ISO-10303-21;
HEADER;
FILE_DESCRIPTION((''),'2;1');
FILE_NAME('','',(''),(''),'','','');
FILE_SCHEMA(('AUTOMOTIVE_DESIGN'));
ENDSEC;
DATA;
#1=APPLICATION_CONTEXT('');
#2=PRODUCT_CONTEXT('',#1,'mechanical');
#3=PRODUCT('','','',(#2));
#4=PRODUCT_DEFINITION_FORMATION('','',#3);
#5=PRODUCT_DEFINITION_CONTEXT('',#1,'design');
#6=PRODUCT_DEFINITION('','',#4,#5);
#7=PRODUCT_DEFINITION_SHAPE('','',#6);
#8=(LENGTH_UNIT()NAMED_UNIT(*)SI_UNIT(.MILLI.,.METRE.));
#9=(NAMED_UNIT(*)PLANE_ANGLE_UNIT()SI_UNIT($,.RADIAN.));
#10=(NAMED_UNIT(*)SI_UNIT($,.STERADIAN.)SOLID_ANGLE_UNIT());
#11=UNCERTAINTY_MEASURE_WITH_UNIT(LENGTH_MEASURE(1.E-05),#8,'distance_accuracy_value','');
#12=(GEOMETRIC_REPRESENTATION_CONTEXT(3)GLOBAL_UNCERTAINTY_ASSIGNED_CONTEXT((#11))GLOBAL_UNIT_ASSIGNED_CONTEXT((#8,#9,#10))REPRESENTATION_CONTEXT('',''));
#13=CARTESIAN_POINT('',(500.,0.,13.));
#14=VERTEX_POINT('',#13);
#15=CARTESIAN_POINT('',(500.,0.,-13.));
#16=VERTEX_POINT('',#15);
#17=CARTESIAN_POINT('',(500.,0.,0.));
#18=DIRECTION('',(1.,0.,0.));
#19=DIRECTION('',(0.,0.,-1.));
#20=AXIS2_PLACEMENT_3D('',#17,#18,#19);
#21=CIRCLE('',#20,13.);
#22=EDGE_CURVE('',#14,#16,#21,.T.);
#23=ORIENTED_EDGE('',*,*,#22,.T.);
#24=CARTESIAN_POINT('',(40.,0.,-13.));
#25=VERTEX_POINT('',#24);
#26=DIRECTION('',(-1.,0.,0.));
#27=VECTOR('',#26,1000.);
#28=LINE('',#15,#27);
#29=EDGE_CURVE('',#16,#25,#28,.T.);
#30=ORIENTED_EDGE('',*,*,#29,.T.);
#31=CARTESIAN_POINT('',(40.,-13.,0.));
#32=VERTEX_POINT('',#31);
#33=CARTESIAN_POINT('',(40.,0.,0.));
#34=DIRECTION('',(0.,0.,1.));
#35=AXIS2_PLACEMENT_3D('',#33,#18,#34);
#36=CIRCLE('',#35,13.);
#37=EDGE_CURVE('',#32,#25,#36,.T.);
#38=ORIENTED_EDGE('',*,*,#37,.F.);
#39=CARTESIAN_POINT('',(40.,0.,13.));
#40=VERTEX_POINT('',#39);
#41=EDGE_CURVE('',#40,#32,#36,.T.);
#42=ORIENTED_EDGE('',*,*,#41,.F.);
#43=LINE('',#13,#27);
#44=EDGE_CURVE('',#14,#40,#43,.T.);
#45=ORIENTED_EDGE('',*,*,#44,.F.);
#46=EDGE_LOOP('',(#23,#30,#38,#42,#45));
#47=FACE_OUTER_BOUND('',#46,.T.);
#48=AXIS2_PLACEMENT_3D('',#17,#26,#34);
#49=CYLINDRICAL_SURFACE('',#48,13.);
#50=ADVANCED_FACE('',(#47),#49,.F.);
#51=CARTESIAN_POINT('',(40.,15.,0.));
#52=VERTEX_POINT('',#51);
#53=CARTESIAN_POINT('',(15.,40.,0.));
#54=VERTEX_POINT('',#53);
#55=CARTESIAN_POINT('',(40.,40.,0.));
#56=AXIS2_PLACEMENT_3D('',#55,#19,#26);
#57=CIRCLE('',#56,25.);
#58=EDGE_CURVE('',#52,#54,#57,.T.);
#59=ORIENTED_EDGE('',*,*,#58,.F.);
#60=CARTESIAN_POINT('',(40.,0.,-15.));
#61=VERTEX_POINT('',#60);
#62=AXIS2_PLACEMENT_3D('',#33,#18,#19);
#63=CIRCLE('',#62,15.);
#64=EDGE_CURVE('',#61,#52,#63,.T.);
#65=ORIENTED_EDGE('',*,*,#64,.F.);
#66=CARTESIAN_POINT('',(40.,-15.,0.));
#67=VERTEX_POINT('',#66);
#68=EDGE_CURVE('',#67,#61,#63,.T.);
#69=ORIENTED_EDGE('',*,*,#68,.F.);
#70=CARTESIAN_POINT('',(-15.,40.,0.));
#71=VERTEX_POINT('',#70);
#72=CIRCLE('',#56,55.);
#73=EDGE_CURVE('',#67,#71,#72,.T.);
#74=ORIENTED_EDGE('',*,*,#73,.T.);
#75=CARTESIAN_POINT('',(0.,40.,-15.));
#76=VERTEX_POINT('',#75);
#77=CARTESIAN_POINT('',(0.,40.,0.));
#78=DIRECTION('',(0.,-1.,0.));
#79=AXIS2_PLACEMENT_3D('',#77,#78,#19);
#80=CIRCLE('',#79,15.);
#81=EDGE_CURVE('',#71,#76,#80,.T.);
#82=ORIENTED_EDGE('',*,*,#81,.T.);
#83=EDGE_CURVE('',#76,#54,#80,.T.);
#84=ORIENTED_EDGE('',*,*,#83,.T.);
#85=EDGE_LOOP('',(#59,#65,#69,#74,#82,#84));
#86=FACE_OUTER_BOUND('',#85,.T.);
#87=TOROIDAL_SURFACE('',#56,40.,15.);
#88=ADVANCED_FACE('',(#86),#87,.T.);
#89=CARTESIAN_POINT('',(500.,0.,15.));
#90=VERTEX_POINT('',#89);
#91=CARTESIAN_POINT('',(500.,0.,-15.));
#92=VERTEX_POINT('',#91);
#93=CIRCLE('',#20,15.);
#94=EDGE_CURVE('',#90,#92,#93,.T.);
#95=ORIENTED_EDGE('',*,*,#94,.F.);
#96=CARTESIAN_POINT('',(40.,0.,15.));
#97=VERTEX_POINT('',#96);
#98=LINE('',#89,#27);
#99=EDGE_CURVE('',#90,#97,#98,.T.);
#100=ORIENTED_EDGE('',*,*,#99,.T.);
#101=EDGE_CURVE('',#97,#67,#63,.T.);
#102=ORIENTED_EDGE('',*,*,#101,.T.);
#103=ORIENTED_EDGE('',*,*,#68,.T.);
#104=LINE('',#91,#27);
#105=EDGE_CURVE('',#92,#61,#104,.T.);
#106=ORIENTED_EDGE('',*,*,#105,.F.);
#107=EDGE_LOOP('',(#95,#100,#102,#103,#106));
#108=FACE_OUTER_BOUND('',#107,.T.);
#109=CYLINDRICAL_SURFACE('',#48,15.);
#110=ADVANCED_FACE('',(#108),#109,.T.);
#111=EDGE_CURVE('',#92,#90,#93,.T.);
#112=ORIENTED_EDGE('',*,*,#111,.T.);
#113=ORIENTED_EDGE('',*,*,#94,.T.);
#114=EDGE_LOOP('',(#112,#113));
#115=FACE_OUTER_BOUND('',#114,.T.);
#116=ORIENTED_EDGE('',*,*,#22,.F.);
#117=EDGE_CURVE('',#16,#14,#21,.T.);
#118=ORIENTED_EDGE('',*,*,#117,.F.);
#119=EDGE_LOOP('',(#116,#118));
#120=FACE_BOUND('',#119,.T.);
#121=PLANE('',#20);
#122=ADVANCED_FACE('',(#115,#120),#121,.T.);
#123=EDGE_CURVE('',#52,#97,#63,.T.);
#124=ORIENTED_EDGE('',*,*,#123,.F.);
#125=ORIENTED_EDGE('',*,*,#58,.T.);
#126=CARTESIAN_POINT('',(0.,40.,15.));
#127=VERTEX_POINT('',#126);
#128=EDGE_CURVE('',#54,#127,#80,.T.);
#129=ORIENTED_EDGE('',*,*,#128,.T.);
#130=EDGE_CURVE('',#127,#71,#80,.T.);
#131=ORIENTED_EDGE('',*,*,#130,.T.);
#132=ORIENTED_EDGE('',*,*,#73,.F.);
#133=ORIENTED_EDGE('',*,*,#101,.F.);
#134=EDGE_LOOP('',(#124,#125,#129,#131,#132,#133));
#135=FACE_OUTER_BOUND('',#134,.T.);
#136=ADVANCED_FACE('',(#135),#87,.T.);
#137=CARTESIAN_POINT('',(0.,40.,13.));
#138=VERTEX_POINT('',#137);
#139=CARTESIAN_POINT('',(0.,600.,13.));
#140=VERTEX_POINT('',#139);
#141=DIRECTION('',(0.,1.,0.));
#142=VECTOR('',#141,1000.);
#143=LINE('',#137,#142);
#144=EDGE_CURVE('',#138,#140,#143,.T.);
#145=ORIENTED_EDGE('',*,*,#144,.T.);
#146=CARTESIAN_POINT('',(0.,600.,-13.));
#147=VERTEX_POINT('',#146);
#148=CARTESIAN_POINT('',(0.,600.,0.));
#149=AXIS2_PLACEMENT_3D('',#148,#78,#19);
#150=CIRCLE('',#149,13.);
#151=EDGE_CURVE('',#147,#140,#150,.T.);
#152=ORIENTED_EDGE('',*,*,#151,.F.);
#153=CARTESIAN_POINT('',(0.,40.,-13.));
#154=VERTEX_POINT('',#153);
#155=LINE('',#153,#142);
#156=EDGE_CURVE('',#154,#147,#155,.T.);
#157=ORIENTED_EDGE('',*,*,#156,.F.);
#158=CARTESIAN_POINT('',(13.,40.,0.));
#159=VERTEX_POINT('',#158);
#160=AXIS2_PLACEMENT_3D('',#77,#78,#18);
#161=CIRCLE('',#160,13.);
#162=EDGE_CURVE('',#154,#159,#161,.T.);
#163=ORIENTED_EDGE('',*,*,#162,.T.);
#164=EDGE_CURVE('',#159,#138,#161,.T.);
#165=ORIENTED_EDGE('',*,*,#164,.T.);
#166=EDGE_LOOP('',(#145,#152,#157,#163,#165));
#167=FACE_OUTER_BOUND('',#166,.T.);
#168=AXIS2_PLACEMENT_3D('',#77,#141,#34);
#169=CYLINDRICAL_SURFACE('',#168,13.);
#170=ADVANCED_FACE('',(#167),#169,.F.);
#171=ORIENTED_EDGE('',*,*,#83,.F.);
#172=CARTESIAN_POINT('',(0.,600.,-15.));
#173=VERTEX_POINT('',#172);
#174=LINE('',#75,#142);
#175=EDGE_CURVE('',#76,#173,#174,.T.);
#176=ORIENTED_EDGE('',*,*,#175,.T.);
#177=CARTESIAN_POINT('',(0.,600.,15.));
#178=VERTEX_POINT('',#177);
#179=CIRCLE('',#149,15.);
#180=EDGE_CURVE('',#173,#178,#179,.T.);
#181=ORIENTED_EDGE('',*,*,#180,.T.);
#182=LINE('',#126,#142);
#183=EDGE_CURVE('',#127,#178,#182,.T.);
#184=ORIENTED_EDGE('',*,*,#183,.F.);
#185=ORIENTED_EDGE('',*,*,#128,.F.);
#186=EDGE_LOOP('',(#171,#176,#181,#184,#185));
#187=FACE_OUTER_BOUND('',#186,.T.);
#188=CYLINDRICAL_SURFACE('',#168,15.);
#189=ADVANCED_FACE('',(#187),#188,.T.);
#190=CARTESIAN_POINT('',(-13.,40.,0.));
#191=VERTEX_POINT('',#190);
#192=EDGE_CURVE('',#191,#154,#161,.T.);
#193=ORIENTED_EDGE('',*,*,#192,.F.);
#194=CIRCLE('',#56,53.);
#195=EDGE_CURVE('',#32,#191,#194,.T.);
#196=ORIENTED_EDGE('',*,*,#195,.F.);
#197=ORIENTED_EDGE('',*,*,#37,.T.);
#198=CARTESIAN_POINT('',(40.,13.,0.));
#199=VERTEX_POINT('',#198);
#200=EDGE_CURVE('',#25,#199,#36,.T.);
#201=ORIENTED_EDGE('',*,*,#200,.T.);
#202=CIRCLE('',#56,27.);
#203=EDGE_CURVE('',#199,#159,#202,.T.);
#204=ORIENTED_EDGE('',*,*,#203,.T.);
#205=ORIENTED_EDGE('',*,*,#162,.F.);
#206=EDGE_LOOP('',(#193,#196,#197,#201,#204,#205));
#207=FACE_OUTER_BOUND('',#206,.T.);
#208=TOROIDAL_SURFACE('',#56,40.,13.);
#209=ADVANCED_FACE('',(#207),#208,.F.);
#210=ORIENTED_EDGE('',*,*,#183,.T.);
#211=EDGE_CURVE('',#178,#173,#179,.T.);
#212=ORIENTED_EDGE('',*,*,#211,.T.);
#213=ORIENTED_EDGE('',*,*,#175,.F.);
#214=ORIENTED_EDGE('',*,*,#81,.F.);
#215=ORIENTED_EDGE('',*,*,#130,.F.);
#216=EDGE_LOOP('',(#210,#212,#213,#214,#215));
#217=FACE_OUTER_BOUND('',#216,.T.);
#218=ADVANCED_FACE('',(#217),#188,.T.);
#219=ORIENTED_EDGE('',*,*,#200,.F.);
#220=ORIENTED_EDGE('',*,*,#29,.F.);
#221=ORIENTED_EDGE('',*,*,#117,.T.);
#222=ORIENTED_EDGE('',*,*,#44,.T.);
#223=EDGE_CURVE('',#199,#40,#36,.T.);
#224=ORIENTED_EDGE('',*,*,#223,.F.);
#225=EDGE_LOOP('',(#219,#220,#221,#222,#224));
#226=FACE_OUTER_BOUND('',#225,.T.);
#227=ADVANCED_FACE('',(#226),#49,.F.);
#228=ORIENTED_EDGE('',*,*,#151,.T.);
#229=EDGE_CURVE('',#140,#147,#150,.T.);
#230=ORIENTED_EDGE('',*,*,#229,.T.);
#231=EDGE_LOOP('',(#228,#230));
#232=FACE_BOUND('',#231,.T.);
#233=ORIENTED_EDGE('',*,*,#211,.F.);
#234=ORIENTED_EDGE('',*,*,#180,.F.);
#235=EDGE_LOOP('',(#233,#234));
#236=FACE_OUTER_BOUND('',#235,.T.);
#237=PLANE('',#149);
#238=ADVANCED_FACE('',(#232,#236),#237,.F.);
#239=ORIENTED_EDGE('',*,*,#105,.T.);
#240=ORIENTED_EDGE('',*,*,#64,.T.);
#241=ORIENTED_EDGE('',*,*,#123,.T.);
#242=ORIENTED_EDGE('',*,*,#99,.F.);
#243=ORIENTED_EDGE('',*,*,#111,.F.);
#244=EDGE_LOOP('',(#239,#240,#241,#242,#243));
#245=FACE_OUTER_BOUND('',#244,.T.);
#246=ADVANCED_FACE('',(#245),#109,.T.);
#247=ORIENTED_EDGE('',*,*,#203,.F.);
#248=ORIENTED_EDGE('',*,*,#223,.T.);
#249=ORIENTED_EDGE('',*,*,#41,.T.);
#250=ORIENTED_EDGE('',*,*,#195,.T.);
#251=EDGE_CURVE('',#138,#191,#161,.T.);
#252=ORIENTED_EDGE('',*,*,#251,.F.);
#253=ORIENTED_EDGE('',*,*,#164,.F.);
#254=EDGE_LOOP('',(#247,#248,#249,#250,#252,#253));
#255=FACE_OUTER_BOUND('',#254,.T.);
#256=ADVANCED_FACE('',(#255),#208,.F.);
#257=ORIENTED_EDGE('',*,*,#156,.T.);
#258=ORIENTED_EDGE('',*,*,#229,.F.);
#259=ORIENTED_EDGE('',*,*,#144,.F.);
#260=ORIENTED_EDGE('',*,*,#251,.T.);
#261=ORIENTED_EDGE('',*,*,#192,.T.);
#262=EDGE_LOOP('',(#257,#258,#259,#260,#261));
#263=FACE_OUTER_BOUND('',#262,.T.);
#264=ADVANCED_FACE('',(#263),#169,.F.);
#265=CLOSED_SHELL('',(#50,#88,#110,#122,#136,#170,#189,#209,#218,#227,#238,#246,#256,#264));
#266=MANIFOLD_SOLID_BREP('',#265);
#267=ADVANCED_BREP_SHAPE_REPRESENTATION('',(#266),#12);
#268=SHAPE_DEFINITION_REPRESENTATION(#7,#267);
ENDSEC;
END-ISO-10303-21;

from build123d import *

# Parameters (mm, degrees)
SWEEP_THIN1_PROFILE_R   = 15
SWEEP_THIN1_PROFILE_R_2 = 13


with BuildPart() as part:
    # Sweep-Thin1: sweep along a path in Sketch1
    with BuildLine(Plane.XY) as sweep_thin1_path:
        Line((500, 0), (40, 0))
        ThreePointArc((40, 0), (11.715728753, 11.715728753), (0, 40))
        Line((0, 40), (0, 600))
    # Sweep-Thin1 profile (on start of the path) → Sweep-Thin1 (sweep)
    with BuildSketch(Plane(origin=(500, 0, 0), x_dir=(0, 0, -1), z_dir=(-1, 0, 0))):
        Circle(SWEEP_THIN1_PROFILE_R)
        Circle(SWEEP_THIN1_PROFILE_R_2, mode=Mode.SUBTRACT)
    sweep(path=sweep_thin1_path.line)


solid = part.part
